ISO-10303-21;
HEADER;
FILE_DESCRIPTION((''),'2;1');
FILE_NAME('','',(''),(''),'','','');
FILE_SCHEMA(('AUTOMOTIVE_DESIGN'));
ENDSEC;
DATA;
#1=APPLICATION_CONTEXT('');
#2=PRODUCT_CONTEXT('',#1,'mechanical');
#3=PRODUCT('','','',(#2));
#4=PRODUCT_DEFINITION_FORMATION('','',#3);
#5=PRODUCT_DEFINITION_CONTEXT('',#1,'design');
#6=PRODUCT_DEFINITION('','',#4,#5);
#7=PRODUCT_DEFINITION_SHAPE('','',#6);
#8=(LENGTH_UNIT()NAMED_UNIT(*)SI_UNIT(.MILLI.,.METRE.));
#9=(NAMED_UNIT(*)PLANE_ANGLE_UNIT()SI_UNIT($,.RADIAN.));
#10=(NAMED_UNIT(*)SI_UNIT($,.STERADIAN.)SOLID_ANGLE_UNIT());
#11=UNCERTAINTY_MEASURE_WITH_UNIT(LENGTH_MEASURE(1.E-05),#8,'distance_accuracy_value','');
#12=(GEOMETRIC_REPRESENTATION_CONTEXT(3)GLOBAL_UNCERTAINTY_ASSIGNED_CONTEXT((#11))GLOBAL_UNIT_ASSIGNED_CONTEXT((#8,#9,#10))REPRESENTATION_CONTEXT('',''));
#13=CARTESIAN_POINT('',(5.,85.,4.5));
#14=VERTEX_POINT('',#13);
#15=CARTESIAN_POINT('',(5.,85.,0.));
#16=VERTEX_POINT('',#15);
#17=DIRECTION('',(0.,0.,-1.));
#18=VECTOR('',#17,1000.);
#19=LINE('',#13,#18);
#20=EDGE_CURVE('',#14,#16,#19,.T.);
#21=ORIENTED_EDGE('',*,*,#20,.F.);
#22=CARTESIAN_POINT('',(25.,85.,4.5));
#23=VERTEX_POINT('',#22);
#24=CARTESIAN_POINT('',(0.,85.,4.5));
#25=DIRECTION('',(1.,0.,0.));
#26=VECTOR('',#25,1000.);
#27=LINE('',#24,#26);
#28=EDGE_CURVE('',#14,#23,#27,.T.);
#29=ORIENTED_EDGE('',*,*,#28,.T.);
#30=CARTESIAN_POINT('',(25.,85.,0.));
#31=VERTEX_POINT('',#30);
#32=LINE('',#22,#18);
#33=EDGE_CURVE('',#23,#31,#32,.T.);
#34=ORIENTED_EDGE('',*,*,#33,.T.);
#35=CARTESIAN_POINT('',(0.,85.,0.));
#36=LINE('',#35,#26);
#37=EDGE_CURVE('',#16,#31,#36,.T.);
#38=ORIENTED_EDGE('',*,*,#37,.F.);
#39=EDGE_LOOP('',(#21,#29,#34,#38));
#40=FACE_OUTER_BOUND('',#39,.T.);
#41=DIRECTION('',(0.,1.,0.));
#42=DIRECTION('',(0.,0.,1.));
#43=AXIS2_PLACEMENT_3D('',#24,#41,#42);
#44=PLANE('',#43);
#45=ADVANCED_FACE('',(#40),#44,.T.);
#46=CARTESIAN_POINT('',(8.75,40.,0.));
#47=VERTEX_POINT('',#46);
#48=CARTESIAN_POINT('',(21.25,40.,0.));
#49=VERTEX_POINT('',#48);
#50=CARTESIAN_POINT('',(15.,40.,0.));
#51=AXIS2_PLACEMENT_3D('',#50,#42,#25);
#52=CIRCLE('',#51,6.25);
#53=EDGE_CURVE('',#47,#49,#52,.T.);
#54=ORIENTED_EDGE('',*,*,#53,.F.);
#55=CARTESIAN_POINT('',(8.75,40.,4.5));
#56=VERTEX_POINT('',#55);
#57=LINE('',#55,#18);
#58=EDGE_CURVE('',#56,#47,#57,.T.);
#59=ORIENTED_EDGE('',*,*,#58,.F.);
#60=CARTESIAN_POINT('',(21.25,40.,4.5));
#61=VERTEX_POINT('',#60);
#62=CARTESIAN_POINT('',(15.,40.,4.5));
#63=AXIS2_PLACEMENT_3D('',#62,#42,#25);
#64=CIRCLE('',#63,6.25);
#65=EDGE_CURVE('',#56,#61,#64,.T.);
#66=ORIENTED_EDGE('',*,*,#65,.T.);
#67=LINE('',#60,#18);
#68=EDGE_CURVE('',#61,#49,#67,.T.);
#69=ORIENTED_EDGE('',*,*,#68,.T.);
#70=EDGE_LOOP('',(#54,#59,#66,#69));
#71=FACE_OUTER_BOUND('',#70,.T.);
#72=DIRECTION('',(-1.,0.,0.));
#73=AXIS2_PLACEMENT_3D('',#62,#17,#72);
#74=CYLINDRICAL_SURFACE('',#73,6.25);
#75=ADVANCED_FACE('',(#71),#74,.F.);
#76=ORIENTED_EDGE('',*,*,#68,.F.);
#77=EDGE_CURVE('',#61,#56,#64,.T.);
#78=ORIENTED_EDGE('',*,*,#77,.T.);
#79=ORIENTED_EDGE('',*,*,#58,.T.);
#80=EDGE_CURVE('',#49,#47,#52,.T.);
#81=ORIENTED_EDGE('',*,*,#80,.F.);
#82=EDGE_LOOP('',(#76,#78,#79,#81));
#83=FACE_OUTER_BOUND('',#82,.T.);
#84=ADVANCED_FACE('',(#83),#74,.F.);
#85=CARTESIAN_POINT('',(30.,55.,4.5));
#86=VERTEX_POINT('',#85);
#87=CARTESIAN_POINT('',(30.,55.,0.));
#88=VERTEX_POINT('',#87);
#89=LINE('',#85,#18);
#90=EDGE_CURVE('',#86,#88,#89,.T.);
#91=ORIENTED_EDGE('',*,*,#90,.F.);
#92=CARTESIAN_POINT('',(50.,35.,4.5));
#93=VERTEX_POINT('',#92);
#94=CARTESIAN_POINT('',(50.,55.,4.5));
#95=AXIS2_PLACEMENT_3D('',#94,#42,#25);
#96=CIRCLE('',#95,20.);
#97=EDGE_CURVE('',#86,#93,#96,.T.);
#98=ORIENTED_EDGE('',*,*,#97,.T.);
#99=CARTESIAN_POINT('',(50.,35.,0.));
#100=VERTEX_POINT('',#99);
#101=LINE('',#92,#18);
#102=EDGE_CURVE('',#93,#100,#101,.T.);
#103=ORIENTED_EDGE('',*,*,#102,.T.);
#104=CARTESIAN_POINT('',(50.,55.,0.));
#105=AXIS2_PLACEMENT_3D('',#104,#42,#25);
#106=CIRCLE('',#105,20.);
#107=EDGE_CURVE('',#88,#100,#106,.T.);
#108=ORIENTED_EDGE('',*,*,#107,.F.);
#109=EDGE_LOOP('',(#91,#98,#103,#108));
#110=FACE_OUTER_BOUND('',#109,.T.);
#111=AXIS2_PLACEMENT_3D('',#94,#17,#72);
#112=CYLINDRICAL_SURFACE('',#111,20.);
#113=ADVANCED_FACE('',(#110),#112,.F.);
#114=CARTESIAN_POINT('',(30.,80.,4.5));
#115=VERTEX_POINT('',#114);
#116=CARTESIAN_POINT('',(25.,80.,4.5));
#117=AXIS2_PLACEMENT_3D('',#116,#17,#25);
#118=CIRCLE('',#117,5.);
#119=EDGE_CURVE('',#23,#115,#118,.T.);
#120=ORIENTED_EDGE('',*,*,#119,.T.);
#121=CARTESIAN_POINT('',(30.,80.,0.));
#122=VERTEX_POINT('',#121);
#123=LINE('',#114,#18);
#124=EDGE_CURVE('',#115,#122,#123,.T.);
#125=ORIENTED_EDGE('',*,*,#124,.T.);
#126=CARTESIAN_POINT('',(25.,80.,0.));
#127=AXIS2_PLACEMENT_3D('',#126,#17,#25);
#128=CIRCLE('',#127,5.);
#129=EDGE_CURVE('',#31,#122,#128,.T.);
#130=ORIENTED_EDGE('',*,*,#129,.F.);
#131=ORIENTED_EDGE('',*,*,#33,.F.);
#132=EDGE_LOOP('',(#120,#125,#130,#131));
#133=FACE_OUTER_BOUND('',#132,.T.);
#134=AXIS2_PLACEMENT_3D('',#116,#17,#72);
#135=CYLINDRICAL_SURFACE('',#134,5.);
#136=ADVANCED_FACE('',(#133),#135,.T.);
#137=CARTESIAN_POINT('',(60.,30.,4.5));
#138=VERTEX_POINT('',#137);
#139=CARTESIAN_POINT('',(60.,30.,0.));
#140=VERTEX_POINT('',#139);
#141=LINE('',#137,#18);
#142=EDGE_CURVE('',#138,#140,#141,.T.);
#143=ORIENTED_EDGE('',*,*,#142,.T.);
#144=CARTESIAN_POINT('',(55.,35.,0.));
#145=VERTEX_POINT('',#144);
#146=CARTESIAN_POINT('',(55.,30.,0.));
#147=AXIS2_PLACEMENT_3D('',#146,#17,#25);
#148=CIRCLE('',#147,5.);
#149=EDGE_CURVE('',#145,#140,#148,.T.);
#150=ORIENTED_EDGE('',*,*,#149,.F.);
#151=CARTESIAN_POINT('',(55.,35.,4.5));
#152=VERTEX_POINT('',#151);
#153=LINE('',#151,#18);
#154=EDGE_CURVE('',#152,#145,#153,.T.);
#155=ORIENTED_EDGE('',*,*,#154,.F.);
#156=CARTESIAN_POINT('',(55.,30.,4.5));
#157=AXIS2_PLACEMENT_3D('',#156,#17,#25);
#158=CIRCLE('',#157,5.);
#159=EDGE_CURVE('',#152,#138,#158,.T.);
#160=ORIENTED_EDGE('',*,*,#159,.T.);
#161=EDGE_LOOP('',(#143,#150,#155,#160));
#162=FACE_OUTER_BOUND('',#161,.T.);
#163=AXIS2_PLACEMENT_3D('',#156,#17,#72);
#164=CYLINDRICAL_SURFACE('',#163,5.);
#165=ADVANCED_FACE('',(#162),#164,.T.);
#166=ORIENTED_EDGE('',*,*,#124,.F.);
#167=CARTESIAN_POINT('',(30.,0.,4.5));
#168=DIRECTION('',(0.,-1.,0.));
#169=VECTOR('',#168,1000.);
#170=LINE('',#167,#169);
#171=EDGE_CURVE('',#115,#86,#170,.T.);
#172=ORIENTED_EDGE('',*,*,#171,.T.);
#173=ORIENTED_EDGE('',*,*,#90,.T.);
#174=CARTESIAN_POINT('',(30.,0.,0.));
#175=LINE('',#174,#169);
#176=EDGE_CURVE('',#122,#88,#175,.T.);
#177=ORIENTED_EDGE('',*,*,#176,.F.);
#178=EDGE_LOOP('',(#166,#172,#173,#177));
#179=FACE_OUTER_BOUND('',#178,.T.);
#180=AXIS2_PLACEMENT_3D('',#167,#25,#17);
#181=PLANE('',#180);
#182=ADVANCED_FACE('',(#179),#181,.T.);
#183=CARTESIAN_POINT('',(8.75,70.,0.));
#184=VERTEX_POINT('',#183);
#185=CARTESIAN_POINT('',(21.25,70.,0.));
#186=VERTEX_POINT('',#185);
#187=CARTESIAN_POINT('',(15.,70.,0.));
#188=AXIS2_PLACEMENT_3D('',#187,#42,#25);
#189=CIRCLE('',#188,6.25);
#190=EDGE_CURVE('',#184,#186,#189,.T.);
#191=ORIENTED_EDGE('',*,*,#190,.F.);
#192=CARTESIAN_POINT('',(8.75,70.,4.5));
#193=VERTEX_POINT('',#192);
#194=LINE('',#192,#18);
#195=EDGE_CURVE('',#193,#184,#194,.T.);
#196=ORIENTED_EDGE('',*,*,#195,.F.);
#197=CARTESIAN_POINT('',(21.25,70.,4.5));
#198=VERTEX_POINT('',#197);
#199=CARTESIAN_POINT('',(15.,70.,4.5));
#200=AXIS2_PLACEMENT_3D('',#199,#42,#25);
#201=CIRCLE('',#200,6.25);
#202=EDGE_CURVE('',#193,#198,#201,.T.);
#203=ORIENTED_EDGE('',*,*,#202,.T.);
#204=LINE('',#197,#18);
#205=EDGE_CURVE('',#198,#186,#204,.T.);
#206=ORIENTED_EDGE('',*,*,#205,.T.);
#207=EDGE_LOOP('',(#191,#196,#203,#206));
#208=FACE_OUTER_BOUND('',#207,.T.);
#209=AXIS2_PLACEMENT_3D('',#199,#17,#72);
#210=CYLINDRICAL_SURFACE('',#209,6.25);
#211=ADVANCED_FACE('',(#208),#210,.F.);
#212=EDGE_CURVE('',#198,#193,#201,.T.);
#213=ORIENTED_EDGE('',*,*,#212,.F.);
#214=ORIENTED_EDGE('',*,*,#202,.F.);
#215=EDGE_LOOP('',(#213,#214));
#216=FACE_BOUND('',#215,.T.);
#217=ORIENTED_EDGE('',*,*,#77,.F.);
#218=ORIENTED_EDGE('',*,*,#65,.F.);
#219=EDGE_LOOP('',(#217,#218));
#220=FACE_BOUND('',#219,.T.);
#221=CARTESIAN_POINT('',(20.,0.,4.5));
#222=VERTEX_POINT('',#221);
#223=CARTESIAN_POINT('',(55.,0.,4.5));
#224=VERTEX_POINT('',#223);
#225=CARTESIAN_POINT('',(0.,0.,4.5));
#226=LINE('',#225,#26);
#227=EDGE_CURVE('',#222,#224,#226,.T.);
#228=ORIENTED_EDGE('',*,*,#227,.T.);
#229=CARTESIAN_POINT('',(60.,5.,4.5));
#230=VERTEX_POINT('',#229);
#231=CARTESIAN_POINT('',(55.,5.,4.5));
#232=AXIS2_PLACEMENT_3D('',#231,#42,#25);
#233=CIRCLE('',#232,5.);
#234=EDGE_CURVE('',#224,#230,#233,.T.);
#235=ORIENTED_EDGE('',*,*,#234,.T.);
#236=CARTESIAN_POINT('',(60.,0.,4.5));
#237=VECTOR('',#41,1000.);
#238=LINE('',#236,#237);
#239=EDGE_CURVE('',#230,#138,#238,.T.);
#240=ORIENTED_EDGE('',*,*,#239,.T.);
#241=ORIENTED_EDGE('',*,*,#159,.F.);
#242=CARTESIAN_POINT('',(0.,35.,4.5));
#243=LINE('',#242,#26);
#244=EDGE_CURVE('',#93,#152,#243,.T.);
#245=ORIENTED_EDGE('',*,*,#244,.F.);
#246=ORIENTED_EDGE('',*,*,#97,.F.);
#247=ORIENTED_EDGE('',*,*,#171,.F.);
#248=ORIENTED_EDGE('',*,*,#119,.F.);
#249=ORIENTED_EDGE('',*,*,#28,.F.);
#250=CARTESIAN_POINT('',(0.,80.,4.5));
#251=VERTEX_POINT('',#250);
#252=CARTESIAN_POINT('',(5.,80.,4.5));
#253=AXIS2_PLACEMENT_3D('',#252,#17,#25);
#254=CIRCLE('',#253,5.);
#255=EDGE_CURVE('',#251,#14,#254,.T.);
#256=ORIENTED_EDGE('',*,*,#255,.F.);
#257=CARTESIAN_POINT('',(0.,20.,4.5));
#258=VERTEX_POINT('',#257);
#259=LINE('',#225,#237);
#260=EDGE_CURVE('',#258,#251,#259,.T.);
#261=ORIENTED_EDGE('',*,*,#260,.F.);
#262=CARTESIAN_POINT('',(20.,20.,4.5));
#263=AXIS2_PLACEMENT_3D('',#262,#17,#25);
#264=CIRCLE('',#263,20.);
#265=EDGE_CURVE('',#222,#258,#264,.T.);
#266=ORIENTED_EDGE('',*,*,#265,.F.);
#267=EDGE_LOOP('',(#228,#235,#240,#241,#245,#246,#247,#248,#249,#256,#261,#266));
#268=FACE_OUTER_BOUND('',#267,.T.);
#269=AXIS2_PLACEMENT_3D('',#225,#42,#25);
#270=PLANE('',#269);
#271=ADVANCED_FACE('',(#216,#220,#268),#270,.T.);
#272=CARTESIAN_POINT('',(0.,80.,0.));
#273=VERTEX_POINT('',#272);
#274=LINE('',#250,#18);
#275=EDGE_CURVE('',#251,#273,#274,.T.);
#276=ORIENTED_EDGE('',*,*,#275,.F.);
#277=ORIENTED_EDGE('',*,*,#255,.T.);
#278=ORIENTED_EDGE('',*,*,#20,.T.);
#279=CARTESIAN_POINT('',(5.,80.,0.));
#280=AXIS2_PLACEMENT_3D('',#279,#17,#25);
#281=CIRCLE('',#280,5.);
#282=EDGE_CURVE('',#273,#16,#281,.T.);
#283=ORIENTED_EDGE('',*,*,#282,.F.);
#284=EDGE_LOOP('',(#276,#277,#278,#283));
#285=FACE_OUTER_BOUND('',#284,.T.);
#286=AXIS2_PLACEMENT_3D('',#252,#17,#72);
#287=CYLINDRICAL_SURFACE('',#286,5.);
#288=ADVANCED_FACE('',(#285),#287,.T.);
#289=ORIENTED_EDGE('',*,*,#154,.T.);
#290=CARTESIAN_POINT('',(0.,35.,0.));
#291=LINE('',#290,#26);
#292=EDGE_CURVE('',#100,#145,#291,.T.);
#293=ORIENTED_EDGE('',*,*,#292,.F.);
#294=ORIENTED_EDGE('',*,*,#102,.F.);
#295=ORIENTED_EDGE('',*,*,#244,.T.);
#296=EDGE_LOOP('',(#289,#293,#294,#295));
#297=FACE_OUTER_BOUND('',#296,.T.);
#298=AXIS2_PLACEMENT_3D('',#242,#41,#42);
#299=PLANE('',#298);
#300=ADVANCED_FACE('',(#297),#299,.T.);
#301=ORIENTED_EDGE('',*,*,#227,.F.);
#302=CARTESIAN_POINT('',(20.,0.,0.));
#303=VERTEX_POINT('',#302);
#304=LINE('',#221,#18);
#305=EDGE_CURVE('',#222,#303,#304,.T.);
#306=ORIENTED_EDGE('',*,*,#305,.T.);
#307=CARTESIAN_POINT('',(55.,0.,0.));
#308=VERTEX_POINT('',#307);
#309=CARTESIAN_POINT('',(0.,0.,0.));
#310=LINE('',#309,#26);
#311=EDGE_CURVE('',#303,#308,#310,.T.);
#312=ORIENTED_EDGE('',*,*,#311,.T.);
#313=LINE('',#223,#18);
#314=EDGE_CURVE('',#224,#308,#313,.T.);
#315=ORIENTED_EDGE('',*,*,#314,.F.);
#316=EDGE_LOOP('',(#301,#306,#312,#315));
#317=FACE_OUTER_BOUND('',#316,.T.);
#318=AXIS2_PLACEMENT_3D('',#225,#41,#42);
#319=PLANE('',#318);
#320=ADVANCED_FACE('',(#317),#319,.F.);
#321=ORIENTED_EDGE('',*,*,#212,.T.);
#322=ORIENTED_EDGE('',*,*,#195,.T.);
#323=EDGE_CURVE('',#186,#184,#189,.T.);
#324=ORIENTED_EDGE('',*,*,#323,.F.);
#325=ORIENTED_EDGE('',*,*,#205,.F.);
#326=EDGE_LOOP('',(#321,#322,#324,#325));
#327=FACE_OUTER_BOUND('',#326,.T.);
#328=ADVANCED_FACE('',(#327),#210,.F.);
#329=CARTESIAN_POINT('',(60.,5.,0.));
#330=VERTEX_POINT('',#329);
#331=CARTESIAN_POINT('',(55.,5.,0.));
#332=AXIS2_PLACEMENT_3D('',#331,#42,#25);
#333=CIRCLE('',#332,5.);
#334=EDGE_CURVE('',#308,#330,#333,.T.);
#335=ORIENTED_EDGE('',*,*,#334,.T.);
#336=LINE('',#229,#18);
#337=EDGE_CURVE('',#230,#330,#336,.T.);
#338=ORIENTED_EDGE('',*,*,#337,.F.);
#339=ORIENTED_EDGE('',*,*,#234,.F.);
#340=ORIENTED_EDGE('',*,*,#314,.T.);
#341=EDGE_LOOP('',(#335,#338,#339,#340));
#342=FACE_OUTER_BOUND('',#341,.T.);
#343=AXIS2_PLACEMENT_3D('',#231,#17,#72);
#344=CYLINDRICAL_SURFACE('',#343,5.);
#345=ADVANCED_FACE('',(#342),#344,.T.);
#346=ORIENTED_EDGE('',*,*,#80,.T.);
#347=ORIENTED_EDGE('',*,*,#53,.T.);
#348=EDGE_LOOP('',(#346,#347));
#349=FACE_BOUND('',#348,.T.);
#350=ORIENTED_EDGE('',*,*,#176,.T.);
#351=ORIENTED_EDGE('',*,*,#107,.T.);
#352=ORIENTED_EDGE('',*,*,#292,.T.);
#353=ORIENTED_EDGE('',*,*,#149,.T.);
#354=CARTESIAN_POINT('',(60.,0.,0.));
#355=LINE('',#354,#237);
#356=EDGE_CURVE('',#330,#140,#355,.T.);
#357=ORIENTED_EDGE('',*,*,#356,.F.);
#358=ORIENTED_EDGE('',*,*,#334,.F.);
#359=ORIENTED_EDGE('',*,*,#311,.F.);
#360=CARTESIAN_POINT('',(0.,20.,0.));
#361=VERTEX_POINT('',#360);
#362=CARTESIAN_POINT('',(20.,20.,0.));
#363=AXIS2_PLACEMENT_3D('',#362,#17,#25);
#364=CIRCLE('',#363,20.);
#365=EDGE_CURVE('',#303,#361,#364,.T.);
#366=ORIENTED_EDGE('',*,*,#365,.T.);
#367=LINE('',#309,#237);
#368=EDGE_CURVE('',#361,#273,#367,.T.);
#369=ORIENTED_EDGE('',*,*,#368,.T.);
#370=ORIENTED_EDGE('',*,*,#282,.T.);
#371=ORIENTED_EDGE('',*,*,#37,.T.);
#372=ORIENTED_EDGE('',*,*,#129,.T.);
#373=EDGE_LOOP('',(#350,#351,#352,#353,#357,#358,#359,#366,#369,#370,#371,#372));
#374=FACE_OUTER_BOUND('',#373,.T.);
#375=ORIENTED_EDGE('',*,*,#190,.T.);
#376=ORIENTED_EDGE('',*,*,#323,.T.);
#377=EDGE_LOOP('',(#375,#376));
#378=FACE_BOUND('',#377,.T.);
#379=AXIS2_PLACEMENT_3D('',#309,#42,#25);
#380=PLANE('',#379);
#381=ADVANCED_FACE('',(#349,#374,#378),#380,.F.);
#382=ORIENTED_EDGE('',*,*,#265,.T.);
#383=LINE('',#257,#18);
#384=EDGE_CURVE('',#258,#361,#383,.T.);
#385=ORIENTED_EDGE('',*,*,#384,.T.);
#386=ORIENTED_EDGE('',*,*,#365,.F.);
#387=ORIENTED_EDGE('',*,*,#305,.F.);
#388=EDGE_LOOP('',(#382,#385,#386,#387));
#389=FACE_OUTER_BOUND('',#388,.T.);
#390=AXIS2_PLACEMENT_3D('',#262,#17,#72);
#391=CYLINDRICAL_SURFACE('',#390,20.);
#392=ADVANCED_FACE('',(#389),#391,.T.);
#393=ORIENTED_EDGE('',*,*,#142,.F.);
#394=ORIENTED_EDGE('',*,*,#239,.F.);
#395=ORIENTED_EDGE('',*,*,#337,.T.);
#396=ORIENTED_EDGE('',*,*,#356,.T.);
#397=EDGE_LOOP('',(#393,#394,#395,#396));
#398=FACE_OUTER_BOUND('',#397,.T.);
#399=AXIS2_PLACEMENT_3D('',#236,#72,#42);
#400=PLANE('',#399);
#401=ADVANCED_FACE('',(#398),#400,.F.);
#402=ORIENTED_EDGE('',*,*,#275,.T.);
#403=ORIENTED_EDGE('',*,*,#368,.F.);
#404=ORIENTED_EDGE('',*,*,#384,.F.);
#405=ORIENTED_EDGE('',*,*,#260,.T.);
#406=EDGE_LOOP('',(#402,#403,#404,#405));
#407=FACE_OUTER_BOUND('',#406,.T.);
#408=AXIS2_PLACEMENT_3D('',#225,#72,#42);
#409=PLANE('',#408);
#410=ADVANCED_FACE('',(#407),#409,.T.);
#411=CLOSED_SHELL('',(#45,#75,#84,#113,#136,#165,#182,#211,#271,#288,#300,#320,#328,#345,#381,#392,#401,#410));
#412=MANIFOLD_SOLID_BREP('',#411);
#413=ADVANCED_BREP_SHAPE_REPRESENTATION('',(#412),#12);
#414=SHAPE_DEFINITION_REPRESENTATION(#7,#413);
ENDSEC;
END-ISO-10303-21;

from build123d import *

# Parameters (mm, degrees)
SKETCH1_R           = 6.25
BOSS_EXTRUDE1_DEPTH = 4.5


with BuildPart() as part:
    # Sketch1 → Boss-Extrude1 (new body)
    with BuildSketch(Plane.XY):
        with BuildLine():
            Line((25, 85), (5, 85))
            ThreePointArc((5, 85), (1.464466094, 83.535533906), (0, 80))
            Line((0, 80), (0, 20))
            ThreePointArc((0, 20), (5.857864376, 5.857864376), (20, 0))
            Line((20, 0), (55, 0))
            ThreePointArc((55, 0), (58.535533906, 1.464466094), (60, 5))
            Line((60, 5), (60, 30))
            ThreePointArc((60, 30), (58.535533906, 33.535533906), (55, 35))
            Line((55, 35), (50, 35))
            ThreePointArc((50, 35), (35.857864376, 40.857864376), (30, 55))
            Line((30, 55), (30, 80))
            ThreePointArc((30, 80), (28.535533906, 83.535533906), (25, 85))
        make_face()
        with Locations((15, 40)):
            Circle(SKETCH1_R, mode=Mode.SUBTRACT)
        with Locations((15, 70)):
            Circle(SKETCH1_R, mode=Mode.SUBTRACT)
    extrude(amount=BOSS_EXTRUDE1_DEPTH)


solid = part.part
